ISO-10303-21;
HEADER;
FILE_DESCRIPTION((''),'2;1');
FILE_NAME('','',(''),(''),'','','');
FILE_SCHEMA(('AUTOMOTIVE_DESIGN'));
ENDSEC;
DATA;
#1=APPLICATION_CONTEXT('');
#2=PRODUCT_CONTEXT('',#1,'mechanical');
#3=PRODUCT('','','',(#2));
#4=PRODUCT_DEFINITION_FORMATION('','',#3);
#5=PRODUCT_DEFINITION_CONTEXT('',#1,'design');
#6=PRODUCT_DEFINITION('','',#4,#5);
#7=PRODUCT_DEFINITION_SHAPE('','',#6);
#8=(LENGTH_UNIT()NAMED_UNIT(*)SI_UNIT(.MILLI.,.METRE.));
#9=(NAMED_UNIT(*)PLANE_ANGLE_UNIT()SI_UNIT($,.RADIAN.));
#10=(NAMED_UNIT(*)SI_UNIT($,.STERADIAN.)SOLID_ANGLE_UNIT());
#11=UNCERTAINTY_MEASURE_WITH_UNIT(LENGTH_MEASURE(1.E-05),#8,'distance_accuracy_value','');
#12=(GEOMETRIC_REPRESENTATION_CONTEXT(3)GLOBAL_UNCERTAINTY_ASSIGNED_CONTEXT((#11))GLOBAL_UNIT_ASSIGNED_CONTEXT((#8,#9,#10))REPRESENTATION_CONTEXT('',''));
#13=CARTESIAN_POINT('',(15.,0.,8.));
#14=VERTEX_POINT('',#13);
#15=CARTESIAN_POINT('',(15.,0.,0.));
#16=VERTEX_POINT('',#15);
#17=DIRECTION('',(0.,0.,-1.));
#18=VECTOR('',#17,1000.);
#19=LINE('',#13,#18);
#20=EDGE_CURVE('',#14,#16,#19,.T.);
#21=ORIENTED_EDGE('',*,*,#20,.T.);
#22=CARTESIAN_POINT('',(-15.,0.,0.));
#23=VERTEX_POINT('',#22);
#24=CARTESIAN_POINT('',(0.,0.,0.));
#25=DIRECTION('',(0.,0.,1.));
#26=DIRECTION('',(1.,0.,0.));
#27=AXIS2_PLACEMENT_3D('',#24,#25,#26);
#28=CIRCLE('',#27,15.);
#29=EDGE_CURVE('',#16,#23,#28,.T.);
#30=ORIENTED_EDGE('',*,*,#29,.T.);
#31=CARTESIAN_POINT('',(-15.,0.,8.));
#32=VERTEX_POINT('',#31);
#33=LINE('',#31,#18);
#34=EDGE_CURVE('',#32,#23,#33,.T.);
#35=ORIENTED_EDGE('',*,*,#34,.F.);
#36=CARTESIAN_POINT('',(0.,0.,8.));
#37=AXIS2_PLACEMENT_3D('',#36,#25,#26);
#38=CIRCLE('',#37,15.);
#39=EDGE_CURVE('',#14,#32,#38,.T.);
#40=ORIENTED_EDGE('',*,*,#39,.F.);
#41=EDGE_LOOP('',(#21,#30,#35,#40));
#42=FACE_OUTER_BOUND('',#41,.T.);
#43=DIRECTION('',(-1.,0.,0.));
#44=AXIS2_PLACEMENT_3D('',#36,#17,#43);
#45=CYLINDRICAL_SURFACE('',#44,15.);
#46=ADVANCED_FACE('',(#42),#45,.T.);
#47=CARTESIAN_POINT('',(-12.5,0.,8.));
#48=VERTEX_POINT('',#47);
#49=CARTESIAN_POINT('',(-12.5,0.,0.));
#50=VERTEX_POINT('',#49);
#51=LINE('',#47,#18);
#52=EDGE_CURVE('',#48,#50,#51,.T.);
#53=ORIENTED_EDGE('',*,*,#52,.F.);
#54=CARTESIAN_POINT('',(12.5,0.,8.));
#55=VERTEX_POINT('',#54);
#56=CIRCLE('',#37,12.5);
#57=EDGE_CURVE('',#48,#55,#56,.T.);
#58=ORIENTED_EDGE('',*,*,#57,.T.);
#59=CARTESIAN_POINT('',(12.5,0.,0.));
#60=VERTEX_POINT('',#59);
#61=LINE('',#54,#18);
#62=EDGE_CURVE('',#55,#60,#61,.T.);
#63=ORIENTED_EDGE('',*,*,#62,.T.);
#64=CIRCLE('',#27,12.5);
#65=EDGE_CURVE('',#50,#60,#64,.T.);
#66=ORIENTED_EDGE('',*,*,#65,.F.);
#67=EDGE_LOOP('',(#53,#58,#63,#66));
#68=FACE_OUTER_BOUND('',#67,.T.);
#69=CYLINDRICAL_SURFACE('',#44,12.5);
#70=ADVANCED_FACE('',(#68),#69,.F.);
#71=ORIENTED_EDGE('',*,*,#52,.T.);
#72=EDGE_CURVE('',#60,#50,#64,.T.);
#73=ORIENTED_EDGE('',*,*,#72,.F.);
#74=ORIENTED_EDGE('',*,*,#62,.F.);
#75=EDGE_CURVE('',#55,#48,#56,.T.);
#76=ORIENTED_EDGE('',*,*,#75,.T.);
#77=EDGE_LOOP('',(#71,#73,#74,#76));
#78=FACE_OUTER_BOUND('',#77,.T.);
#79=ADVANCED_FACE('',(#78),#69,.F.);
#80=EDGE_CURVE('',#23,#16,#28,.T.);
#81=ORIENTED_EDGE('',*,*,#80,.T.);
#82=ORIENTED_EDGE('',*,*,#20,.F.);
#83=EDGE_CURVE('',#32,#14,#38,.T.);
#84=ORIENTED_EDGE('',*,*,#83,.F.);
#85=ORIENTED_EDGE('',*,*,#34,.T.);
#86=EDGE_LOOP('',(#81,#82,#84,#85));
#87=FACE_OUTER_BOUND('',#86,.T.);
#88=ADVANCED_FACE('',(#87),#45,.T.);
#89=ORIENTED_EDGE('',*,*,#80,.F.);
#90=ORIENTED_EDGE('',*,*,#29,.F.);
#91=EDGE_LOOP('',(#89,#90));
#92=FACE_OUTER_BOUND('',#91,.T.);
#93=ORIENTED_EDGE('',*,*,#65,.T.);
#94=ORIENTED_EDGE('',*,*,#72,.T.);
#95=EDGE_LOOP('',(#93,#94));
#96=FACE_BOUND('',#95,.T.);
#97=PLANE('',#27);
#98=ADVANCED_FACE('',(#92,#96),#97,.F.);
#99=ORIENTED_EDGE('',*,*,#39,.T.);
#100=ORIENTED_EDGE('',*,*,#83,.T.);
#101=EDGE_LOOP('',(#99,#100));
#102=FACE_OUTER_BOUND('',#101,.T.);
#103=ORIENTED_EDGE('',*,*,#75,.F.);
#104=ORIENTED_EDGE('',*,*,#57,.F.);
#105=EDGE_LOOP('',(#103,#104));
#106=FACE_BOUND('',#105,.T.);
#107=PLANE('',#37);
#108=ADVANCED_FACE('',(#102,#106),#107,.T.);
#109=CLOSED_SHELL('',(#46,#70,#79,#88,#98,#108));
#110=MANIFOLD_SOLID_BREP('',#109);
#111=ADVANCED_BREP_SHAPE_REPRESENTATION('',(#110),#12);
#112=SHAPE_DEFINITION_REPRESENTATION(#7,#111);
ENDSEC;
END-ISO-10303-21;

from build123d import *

# Parameters (mm, degrees)
SKETCH_1_R      = 15
SKETCH_1_R_2    = 12.5
EXTRUDE_1_DEPTH = 8


with BuildPart() as part:
    # 草图1 → 凸台-拉伸1 (new body)
    with BuildSketch(Plane.XY):
        Circle(SKETCH_1_R)
        Circle(SKETCH_1_R_2, mode=Mode.SUBTRACT)
    extrude(amount=EXTRUDE_1_DEPTH)


solid = part.part
